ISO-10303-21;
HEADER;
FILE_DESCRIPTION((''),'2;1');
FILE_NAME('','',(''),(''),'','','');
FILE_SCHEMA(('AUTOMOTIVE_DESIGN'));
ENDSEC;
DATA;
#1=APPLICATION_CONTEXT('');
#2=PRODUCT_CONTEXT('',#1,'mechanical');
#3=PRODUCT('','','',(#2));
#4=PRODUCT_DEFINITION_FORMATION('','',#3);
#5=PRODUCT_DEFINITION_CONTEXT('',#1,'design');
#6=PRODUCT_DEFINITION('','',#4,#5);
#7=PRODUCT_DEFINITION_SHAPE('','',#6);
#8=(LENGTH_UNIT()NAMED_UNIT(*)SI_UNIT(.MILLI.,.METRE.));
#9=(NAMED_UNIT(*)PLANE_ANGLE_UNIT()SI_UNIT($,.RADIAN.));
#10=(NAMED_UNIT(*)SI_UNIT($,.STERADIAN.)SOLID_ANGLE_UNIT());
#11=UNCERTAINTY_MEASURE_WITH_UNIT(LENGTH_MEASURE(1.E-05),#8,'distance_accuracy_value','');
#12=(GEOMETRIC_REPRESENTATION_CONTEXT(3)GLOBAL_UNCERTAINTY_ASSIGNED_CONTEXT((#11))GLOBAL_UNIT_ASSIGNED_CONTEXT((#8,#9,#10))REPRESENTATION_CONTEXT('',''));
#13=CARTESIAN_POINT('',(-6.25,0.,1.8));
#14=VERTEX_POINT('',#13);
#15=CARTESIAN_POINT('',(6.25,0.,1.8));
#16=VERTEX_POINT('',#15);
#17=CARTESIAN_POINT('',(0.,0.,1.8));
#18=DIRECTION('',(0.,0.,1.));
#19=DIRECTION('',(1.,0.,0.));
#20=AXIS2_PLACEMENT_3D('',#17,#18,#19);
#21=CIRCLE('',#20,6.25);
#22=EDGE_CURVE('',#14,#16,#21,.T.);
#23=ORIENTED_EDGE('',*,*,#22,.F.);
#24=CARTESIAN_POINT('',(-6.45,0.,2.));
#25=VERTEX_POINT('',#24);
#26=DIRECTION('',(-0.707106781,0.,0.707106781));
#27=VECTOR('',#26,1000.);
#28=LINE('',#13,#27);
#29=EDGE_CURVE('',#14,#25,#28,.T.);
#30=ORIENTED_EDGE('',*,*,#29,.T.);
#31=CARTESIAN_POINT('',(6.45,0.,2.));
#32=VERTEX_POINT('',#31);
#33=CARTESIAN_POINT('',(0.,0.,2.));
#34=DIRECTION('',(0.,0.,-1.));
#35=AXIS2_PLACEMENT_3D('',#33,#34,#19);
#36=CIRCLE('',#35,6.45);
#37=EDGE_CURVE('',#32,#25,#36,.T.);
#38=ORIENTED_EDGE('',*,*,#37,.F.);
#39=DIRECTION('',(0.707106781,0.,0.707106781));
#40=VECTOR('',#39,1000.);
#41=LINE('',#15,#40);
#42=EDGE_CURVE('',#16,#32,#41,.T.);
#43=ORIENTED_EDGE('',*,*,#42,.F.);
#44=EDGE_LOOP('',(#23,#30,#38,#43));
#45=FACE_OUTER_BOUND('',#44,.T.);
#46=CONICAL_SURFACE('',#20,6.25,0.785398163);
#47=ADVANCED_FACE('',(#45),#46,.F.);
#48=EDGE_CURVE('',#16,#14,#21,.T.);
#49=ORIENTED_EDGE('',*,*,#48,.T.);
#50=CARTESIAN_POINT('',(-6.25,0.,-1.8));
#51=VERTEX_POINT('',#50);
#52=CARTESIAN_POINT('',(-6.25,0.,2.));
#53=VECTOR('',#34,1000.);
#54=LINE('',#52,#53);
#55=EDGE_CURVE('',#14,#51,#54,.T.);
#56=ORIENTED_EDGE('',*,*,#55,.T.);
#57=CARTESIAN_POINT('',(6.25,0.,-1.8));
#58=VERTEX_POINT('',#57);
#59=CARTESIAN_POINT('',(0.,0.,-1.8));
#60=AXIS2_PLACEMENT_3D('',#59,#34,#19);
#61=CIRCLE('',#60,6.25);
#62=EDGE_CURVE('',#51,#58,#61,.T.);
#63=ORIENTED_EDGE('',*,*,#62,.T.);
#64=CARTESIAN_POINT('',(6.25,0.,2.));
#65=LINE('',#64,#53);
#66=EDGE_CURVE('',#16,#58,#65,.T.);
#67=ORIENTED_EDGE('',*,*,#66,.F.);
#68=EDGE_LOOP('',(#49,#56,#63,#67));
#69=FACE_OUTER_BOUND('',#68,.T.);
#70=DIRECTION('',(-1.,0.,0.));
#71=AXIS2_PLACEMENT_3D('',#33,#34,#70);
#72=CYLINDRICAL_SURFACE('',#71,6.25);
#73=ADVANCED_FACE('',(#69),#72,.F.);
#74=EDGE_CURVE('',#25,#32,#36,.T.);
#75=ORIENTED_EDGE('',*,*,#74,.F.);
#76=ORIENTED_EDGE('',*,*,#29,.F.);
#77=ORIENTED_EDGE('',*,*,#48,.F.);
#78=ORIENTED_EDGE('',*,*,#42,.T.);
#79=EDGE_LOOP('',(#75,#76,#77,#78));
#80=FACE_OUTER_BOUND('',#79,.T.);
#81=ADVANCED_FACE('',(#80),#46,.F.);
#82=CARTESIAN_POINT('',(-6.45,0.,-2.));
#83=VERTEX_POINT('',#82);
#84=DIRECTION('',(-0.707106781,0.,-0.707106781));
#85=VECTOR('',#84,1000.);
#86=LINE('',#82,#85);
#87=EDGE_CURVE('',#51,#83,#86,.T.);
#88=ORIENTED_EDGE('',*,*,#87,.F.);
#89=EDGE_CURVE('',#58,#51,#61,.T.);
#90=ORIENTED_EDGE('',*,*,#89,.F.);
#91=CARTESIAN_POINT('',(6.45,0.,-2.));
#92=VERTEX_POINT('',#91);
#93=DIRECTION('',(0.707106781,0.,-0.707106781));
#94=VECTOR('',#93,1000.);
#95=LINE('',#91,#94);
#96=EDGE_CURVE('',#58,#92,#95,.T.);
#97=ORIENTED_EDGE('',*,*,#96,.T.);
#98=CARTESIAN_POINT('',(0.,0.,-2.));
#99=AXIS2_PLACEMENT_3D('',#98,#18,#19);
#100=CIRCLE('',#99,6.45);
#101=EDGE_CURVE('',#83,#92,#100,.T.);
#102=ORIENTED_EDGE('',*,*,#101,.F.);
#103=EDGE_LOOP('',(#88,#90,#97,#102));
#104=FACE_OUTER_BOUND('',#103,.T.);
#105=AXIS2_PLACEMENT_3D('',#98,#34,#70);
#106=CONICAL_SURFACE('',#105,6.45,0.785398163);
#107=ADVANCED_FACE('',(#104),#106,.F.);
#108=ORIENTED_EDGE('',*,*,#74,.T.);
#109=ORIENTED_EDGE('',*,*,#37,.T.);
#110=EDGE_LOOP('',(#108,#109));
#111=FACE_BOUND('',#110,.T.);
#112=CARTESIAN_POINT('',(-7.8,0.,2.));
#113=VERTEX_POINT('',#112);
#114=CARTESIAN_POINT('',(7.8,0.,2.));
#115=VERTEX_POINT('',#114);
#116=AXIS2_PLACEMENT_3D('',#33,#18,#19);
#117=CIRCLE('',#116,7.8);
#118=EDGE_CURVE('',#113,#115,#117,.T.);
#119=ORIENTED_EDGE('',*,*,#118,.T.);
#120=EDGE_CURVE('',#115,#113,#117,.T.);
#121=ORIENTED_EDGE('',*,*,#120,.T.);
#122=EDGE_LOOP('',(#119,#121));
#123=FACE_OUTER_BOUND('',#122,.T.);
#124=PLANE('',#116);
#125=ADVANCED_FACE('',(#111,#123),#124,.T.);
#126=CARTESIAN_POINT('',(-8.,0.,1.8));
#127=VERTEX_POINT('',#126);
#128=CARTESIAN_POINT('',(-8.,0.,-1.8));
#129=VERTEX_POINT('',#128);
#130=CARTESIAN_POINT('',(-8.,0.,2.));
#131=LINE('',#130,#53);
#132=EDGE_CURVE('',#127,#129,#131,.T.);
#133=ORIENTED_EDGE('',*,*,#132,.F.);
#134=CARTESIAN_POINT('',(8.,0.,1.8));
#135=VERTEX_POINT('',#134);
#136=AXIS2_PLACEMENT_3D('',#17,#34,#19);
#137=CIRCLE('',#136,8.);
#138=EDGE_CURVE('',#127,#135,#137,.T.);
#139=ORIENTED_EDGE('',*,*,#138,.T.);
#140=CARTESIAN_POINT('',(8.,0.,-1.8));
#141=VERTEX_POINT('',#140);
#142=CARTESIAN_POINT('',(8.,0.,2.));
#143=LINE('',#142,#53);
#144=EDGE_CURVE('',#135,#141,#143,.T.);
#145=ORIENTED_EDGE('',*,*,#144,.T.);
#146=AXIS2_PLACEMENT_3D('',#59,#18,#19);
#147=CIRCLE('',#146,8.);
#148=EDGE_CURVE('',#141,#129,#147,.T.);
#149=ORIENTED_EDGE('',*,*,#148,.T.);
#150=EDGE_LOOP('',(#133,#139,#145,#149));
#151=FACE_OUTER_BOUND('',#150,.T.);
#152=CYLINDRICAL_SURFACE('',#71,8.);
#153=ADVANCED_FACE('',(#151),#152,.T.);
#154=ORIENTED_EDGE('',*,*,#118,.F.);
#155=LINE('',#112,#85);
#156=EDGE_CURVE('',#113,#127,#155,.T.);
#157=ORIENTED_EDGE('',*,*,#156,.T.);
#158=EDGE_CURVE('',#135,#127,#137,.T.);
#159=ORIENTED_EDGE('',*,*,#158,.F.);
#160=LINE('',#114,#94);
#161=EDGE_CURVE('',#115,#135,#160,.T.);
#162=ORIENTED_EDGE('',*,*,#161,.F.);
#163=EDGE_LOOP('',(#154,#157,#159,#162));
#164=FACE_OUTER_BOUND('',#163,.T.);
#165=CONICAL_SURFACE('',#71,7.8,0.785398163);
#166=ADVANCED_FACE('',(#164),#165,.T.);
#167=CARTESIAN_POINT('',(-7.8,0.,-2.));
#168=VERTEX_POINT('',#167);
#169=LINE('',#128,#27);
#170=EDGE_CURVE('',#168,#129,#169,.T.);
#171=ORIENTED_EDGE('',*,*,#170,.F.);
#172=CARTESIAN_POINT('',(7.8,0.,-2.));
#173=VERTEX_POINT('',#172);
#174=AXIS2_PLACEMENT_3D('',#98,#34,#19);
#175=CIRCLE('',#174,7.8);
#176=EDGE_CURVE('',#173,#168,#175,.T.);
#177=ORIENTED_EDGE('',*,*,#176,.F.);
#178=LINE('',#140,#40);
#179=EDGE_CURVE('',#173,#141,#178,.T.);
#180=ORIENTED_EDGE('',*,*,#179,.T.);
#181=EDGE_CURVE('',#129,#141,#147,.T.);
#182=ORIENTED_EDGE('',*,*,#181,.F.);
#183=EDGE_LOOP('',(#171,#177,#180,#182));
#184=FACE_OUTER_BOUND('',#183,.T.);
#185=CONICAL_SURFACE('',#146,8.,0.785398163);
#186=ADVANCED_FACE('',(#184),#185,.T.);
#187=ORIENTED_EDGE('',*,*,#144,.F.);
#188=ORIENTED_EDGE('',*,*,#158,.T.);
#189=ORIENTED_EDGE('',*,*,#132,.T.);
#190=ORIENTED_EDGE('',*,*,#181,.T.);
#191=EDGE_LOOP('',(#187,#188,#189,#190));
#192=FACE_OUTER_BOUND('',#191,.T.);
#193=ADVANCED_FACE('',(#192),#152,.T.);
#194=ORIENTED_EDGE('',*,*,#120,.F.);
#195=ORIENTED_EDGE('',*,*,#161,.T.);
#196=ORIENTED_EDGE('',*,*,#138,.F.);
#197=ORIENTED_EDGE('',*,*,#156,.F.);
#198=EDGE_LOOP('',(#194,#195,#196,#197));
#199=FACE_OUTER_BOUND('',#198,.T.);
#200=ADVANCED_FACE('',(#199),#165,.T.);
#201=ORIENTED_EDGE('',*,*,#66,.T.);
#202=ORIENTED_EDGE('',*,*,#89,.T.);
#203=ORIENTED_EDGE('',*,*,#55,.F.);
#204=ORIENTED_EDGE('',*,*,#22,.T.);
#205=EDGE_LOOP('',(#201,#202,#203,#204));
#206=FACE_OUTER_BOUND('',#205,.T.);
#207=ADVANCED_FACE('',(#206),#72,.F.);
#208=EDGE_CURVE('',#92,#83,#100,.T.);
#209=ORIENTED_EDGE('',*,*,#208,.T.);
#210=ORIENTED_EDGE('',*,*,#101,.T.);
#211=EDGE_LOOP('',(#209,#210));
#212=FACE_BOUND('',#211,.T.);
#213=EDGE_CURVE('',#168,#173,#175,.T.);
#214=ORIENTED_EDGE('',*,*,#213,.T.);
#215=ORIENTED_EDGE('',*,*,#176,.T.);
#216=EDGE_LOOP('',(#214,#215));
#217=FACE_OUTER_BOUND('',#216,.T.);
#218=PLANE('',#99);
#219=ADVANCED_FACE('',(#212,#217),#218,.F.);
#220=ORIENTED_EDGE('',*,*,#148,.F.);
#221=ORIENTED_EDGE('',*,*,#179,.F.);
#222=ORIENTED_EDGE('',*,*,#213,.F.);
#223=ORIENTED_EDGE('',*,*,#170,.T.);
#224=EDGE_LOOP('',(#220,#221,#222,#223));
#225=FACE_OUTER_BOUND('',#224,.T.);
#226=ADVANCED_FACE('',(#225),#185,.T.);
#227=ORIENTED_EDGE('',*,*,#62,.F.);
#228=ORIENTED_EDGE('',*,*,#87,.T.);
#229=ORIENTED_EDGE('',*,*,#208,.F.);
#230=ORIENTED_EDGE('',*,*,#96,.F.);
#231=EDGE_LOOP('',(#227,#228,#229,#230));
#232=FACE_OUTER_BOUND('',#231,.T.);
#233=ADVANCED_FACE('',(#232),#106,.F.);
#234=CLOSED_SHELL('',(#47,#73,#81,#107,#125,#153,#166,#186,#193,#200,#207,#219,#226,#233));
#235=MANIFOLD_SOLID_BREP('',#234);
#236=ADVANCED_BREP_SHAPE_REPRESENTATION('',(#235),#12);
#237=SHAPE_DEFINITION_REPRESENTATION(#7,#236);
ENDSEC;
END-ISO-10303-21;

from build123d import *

# Parameters (mm, degrees)
SKETCH1_R           = 8
SKETCH1_R_2         = 6.25
BOSS_EXTRUDE1_DEPTH = 2
CHAMFER1_SIZE       = 0.2


with BuildPart() as part:
    # Sketch1 → Boss-Extrude1 (new, symmetric)
    with BuildSketch(Plane.XY):
        Circle(SKETCH1_R)
        Circle(SKETCH1_R_2, mode=Mode.SUBTRACT)
    extrude(amount=BOSS_EXTRUDE1_DEPTH, both=True)

    # Chamfer1
    chamfer1_edges = [part.edges().sort_by_distance(p)[0] for p in [
        (-8, 0, -2),
        (-8, 0, 2),
        (-6.25, 0, -2),
        (-6.25, 0, 2),
    ]]
    chamfer(chamfer1_edges, length=CHAMFER1_SIZE)


solid = part.part
